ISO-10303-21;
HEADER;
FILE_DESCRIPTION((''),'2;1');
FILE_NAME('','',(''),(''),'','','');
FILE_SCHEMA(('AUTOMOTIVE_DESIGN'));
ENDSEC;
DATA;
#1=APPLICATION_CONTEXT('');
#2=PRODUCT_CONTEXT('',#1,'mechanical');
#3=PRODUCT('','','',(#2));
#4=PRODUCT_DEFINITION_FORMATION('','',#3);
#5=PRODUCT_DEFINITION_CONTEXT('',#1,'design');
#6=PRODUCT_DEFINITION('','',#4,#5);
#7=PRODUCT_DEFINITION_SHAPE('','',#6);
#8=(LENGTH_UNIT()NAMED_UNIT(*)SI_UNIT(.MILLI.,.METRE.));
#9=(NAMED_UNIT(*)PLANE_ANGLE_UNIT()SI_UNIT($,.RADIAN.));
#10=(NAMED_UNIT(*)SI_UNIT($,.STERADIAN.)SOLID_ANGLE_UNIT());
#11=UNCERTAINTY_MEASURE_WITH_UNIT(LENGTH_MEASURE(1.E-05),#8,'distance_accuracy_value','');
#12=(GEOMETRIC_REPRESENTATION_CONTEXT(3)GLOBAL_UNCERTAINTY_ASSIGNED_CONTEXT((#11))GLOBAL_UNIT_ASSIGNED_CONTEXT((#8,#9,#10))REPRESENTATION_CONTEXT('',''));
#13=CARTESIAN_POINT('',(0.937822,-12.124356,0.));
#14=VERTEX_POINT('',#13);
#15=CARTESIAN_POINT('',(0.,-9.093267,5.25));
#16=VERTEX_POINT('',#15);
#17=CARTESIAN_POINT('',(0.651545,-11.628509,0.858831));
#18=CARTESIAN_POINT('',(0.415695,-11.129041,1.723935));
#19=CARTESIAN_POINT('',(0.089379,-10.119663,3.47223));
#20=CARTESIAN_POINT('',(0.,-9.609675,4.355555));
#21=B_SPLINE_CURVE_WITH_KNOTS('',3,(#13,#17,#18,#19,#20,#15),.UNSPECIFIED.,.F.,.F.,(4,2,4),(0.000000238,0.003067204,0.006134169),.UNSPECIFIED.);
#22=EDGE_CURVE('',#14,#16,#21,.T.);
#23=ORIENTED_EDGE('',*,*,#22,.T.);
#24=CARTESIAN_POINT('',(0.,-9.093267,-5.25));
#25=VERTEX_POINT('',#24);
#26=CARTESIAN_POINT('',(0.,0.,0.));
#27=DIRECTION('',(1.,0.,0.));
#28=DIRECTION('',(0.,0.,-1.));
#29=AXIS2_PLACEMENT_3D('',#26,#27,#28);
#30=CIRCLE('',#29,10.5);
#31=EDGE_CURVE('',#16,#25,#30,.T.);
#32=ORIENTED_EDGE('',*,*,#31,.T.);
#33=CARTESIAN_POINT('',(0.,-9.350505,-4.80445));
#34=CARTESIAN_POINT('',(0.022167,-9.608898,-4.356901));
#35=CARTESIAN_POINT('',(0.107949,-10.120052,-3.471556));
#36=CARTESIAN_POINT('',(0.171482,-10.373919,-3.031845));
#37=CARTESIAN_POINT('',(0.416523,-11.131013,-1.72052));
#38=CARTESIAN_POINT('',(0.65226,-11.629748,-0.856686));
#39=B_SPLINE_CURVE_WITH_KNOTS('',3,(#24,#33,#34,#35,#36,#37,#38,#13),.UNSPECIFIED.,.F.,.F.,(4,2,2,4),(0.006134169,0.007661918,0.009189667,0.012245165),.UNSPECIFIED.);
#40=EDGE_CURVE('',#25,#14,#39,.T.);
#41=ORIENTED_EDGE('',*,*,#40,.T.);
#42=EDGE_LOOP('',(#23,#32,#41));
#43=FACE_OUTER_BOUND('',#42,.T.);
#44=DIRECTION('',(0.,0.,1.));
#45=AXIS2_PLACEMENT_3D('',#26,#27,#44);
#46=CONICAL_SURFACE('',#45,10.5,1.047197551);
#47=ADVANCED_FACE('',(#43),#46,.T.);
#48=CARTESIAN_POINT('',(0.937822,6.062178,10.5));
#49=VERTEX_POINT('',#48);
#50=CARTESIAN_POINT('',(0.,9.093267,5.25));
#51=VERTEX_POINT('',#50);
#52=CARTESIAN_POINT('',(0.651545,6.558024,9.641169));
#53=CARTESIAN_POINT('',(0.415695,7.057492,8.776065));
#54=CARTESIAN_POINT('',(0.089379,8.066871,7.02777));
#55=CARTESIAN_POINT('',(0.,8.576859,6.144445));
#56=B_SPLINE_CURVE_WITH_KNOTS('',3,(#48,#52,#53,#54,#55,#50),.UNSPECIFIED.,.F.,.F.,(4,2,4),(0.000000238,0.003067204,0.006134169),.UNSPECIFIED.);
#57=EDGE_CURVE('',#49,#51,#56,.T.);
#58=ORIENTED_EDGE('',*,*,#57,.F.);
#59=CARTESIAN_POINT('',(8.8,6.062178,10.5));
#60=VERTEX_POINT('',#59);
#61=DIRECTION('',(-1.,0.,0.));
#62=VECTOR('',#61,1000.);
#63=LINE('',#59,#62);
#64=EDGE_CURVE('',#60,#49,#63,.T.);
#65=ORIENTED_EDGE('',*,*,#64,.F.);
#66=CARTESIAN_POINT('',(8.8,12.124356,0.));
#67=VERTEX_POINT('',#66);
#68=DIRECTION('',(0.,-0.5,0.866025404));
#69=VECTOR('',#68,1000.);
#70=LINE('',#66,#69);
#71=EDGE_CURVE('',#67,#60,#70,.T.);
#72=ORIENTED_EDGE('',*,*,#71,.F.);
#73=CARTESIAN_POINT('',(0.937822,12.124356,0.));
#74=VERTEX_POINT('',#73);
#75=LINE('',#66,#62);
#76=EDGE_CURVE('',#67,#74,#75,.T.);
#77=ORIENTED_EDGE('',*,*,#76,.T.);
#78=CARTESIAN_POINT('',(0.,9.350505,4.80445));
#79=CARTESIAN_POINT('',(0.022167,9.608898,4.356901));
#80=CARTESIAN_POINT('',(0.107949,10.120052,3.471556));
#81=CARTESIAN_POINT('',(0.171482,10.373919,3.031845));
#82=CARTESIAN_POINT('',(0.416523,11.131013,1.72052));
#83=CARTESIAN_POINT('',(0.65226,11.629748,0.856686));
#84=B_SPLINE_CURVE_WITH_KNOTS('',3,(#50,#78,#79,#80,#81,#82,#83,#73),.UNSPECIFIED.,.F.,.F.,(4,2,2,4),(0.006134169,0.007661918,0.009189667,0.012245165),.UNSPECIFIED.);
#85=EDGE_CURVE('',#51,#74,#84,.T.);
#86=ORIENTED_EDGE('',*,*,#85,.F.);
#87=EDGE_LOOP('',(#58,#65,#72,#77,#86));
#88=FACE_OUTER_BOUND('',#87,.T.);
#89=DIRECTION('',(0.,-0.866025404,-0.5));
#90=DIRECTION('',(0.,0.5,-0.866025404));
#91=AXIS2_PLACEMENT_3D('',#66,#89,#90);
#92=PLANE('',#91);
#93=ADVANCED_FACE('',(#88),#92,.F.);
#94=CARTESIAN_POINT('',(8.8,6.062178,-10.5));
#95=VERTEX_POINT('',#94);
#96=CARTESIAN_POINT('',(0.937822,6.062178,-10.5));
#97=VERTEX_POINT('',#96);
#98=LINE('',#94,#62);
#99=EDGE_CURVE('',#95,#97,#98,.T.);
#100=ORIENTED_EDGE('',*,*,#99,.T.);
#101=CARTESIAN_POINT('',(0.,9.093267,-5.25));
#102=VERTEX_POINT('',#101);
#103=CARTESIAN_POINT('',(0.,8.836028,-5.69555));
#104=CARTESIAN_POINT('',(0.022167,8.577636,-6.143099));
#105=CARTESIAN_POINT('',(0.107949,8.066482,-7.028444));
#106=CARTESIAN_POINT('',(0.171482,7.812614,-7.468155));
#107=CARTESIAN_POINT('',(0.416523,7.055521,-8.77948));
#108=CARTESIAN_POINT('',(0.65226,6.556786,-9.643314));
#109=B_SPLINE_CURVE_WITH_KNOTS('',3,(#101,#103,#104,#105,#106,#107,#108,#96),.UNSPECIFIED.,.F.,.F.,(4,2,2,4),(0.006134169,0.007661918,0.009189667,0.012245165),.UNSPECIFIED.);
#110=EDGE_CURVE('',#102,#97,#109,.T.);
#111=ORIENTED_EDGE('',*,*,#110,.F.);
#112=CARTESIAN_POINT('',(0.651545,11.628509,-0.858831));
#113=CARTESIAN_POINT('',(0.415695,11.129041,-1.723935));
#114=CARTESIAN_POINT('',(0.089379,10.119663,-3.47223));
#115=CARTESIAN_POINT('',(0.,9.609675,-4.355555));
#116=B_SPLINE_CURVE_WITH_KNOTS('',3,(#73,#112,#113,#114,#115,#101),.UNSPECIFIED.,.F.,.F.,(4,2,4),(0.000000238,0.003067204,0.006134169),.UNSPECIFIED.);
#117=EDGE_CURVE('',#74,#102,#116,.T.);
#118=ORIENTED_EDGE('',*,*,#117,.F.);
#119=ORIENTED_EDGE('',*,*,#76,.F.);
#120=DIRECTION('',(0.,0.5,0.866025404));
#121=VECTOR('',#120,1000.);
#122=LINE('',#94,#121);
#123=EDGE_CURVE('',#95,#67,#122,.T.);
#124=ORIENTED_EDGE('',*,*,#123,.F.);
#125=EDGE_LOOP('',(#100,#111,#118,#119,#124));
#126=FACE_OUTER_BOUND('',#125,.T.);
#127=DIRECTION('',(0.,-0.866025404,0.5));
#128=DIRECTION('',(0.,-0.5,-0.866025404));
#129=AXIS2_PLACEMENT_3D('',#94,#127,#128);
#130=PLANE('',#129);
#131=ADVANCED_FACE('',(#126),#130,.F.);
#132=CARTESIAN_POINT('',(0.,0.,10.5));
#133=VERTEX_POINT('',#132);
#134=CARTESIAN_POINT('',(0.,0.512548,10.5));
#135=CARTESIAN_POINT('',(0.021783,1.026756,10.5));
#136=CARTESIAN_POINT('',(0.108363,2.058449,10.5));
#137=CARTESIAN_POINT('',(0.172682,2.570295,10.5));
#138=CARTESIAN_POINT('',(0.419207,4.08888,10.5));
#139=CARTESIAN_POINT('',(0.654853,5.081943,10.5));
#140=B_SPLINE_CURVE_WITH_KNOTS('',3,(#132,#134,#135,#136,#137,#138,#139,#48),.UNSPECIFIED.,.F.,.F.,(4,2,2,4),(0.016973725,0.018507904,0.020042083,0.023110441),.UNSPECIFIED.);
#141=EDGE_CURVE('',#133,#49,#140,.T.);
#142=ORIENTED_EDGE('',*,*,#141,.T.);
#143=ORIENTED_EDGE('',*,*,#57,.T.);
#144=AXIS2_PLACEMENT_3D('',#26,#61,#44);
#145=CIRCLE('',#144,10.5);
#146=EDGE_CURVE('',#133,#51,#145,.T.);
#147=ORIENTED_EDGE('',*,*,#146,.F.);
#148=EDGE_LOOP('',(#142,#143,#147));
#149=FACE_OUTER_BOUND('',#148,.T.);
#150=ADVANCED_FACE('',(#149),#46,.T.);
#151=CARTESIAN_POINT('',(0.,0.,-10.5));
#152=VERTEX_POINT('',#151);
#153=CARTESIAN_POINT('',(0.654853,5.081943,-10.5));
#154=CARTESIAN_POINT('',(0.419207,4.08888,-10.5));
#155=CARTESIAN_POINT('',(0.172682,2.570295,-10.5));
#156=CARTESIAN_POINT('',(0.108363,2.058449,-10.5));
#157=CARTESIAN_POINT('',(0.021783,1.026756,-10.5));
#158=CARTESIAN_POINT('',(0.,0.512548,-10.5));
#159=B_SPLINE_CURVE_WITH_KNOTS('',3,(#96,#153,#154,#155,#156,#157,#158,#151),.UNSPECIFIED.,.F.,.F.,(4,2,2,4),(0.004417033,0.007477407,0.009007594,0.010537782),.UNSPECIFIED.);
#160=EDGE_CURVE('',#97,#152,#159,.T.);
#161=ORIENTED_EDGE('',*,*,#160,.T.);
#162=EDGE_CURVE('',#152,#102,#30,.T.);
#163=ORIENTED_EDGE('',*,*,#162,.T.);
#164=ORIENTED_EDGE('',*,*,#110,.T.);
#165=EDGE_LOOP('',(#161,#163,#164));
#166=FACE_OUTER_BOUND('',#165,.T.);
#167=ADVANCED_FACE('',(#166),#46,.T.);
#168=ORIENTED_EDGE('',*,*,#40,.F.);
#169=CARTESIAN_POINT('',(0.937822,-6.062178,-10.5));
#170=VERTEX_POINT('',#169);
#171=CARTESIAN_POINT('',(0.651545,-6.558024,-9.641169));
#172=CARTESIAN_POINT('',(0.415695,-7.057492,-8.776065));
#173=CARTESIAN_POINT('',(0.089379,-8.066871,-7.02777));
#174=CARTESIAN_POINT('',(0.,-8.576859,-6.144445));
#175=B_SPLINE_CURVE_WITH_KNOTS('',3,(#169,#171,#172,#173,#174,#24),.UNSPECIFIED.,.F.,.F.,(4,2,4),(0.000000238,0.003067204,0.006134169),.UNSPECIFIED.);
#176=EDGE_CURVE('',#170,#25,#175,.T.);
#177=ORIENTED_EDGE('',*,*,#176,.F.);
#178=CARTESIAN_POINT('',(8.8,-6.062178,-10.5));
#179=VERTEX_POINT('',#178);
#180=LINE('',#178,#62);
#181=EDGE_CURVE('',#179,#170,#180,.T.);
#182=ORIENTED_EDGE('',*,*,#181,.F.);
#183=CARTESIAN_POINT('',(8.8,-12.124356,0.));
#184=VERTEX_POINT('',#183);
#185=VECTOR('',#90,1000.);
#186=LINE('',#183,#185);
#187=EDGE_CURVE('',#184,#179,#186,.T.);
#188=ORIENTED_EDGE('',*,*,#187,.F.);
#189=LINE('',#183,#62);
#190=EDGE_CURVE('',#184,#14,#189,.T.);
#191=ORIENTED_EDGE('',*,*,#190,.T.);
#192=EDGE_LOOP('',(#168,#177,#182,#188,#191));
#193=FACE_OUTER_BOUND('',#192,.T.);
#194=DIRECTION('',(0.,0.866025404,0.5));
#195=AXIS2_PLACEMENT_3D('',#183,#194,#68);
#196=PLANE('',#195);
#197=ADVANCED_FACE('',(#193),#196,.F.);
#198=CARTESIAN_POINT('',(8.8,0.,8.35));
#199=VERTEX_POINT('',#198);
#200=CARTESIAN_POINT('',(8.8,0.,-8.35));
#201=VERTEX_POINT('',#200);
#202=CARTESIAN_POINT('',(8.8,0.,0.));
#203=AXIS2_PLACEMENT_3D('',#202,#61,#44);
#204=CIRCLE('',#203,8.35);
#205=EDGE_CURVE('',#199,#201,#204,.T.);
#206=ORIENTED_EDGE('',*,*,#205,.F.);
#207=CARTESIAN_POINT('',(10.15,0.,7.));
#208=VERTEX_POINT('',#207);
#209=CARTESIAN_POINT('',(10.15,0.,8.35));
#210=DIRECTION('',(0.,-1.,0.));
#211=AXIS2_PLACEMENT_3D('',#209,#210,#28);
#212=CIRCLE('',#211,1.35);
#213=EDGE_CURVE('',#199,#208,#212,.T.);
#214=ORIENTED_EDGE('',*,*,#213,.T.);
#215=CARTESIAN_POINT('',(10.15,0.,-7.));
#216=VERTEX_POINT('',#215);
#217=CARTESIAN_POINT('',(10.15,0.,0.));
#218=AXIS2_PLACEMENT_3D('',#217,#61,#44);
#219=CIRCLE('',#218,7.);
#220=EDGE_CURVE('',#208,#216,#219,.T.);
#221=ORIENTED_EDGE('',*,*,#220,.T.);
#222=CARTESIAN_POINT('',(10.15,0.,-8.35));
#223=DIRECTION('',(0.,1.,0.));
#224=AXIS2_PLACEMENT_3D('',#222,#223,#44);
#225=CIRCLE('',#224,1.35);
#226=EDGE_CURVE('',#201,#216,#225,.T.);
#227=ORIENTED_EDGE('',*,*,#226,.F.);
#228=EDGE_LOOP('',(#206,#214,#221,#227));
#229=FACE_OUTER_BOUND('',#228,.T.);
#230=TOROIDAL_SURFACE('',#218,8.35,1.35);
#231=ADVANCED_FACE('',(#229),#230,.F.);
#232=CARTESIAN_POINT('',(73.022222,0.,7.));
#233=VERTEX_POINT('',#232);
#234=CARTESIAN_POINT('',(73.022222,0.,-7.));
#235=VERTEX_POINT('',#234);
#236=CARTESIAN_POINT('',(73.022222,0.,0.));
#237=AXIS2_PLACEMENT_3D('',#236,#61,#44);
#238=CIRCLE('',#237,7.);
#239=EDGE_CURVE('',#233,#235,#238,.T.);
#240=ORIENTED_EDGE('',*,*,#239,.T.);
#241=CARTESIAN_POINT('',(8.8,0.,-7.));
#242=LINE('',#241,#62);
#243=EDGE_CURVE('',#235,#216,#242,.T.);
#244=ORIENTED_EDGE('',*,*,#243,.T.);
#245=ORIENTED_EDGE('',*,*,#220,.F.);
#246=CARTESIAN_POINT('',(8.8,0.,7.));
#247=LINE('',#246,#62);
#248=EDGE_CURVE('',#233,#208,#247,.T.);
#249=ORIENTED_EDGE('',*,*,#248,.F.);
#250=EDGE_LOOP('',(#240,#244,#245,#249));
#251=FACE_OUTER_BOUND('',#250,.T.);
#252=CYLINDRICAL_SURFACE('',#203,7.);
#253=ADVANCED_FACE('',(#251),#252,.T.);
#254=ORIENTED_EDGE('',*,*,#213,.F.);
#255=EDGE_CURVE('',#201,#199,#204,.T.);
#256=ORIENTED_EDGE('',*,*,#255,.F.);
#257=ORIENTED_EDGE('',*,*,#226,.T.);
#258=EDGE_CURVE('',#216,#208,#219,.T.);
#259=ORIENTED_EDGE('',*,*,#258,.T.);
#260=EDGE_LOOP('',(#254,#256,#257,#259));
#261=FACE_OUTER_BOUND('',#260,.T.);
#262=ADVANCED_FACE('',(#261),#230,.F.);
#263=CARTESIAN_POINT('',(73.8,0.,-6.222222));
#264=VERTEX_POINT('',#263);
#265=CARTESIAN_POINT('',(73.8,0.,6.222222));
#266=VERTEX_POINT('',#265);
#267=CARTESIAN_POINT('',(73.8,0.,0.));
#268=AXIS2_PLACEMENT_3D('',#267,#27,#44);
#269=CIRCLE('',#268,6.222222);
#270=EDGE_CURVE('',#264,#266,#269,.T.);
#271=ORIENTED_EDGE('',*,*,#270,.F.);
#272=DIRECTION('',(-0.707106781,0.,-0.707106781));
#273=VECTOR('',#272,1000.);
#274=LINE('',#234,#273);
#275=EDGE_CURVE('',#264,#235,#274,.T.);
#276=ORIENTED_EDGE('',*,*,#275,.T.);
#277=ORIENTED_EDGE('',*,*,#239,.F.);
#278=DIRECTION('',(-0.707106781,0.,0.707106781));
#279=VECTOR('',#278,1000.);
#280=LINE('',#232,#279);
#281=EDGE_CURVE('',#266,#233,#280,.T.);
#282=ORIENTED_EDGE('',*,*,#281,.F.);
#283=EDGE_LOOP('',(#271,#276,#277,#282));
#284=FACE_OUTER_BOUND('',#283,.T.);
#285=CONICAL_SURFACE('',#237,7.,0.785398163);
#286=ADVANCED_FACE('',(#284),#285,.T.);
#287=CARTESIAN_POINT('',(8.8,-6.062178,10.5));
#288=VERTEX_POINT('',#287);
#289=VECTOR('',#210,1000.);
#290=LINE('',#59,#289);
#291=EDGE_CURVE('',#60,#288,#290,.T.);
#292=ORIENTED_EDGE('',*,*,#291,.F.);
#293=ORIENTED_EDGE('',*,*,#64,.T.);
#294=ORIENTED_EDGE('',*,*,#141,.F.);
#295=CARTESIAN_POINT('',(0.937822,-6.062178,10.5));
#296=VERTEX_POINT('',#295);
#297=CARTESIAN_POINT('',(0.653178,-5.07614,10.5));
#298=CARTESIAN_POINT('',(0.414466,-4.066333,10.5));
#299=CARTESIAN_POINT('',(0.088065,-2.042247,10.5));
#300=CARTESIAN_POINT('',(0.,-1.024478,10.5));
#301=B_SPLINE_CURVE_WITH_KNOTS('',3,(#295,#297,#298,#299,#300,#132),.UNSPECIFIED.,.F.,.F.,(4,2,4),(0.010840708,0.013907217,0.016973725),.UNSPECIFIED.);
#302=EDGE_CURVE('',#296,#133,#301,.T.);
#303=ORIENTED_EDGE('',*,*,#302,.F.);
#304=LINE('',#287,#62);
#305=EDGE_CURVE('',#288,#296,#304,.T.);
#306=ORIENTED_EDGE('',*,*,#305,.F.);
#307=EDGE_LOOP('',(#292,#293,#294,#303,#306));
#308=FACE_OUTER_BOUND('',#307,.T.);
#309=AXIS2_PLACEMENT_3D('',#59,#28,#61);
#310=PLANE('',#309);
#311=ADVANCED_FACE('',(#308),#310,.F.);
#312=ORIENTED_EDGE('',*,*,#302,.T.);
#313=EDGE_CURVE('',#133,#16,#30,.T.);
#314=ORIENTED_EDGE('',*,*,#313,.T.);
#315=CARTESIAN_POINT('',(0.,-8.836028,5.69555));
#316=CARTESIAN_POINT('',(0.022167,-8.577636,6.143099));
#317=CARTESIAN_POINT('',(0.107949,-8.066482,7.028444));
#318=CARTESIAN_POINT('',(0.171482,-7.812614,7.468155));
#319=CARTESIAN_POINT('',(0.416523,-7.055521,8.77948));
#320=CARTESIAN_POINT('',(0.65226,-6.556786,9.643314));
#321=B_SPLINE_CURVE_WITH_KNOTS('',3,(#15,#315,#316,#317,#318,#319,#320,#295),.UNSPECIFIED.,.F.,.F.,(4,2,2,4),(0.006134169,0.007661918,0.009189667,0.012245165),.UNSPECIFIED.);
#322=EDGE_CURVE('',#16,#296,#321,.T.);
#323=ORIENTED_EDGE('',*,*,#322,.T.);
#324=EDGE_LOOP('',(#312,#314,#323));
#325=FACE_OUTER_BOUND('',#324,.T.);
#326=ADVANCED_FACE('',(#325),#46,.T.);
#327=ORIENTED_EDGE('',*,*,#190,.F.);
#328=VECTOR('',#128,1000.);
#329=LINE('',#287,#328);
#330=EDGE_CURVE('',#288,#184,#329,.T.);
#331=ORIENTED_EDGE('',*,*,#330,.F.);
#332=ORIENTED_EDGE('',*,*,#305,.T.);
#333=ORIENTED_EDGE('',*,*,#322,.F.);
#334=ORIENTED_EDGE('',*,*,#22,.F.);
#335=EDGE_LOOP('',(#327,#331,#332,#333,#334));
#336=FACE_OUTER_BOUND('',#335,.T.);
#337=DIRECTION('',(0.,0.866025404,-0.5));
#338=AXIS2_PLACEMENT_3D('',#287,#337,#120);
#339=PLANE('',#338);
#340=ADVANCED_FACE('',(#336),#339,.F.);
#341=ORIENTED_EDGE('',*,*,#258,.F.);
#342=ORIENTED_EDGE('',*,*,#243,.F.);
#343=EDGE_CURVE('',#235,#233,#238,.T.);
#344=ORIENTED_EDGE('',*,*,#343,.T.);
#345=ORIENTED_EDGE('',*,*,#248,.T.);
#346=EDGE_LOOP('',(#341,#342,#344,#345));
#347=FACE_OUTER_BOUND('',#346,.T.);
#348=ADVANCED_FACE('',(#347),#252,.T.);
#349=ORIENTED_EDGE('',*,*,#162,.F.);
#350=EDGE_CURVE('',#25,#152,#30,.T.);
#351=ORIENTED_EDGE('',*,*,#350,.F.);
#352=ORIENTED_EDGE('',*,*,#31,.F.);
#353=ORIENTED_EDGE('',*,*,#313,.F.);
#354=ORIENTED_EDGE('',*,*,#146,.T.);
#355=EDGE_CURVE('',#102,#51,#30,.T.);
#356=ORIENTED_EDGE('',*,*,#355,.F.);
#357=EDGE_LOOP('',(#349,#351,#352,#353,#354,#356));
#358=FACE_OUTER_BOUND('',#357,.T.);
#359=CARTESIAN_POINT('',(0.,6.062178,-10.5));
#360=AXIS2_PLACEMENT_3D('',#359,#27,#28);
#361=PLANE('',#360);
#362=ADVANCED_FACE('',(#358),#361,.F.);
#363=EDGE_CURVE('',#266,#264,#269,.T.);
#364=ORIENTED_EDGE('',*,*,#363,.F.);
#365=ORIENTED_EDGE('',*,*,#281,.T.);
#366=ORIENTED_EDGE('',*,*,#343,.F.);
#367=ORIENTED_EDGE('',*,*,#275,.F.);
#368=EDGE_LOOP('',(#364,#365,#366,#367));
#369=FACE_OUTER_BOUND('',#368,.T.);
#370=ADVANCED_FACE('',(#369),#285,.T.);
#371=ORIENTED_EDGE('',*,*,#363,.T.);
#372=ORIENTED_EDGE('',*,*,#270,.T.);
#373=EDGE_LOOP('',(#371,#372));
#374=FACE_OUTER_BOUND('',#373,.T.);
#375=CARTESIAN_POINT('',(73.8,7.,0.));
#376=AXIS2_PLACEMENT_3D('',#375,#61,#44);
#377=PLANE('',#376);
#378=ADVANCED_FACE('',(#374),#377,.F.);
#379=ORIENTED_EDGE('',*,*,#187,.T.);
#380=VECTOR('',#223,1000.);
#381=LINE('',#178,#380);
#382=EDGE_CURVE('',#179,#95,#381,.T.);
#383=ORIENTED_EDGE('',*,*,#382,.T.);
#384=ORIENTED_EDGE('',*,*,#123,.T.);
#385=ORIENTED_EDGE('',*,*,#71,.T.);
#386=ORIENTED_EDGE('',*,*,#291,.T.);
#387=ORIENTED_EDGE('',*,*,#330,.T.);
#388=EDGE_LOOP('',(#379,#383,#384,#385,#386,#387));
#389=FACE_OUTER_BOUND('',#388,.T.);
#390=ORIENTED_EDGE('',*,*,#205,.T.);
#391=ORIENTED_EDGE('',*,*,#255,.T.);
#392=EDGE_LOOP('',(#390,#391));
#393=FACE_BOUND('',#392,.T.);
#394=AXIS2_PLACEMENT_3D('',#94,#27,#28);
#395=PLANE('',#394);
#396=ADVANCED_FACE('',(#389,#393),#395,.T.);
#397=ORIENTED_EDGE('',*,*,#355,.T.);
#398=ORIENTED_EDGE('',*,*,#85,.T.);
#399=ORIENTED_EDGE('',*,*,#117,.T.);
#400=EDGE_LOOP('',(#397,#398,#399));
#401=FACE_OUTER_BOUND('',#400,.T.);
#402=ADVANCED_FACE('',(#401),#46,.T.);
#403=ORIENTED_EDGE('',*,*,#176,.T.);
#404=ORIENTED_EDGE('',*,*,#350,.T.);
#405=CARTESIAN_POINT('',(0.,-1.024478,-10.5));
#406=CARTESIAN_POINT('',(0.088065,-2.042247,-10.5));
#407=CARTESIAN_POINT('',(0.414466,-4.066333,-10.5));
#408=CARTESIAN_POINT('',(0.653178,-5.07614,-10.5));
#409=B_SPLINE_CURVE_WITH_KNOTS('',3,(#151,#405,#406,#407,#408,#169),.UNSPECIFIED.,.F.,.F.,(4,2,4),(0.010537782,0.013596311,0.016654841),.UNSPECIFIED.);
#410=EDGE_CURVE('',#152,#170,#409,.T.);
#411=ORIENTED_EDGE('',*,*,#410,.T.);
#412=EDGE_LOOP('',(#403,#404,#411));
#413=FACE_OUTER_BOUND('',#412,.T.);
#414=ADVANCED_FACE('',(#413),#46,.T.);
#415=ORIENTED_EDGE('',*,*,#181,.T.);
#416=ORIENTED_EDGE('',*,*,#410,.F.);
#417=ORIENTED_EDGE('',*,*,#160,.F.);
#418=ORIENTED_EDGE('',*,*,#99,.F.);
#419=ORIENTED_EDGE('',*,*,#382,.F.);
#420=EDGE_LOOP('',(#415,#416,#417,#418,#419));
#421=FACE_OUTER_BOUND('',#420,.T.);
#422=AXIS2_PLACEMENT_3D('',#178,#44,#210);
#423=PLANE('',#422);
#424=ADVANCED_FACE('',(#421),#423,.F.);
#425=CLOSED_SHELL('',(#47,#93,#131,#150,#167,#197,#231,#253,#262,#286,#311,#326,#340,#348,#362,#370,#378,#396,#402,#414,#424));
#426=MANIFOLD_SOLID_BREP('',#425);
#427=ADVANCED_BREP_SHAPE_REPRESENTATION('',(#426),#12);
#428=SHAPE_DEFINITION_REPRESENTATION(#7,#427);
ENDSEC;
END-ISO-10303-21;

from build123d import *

# Parameters (mm, degrees)
BOSS_EXTRUDE1_DEPTH = 8.8
SKETCH4_R           = 22.78
SKETCH4_R_2         = 10.5
CUT_EXTRUDE1_DEPTH  = 1.1
CUT_EXTRUDE1_DRAFT  = -60
CHAMFER2_SIZE       = 0.777777778


with BuildPart() as part:
    # Sketch3 → Boss-Extrude1 (new body)
    with BuildSketch(Plane(origin=(0, 0, 0), x_dir=(0, 0, -1), z_dir=(1, 0, 0))):
        Polygon((10.5, 6.062177826), (0, 12.124355653), (-10.5, 6.062177826), (-10.5, -6.062177826), (0, -12.124355653), (10.5, -6.062177826), align=None)
    extrude(amount=BOSS_EXTRUDE1_DEPTH)


with BuildPart() as cut_extrude1_tool:
    # Sketch4 → Cut-Extrude1 (with draft: the straight prism first)
    with BuildSketch(Plane.ZY):
        Circle(SKETCH4_R)
        Circle(SKETCH4_R_2, mode=Mode.SUBTRACT)
    extrude(amount=-CUT_EXTRUDE1_DEPTH)
    # Cut-Extrude1: the draft: its side faces are tilted about the plane it starts from
    cut_extrude1_sides = [cut_extrude1_tool.faces().sort_by_distance(p)[0] for p in [
        (0.55, 0, -22.78),
        (0.55, 0, -10.5),
    ]]
    draft(cut_extrude1_sides, Plane.ZY, CUT_EXTRUDE1_DRAFT)


with BuildPart() as part_1:
    add(part.part)

    # Cut-Extrude1: cut by cut_extrude1_tool
    add(cut_extrude1_tool.part, mode=Mode.SUBTRACT)

    # Sketch5 → Revolve1 (revolve)
    with BuildSketch(Plane.XY, mode=Mode.PRIVATE) as revolve1_sk:
        with BuildLine():
            Line((10.15, 7), (73.8, 7))
            Line((73.8, 7), (73.8, 0))
            Line((73.8, 0), (8.8, 0))
            Line((8.8, 0), (8.8, 8.35))
            ThreePointArc((8.8, 8.35), (9.195405845, 7.395405845), (10.15, 7))
        make_face()
    revolve(revolve1_sk.sketch.rotate(Axis((8.8, 0, 0), (1, 0, 0)), 90), axis=Axis((8.8, 0, 0), (1, 0, 0)))

    # Chamfer2
    chamfer2_edges = [part_1.edges().sort_by_distance(p)[0] for p in [
        (73.8, 0, -7),
    ]]
    chamfer(chamfer2_edges, length=CHAMFER2_SIZE)


solid = part_1.part
